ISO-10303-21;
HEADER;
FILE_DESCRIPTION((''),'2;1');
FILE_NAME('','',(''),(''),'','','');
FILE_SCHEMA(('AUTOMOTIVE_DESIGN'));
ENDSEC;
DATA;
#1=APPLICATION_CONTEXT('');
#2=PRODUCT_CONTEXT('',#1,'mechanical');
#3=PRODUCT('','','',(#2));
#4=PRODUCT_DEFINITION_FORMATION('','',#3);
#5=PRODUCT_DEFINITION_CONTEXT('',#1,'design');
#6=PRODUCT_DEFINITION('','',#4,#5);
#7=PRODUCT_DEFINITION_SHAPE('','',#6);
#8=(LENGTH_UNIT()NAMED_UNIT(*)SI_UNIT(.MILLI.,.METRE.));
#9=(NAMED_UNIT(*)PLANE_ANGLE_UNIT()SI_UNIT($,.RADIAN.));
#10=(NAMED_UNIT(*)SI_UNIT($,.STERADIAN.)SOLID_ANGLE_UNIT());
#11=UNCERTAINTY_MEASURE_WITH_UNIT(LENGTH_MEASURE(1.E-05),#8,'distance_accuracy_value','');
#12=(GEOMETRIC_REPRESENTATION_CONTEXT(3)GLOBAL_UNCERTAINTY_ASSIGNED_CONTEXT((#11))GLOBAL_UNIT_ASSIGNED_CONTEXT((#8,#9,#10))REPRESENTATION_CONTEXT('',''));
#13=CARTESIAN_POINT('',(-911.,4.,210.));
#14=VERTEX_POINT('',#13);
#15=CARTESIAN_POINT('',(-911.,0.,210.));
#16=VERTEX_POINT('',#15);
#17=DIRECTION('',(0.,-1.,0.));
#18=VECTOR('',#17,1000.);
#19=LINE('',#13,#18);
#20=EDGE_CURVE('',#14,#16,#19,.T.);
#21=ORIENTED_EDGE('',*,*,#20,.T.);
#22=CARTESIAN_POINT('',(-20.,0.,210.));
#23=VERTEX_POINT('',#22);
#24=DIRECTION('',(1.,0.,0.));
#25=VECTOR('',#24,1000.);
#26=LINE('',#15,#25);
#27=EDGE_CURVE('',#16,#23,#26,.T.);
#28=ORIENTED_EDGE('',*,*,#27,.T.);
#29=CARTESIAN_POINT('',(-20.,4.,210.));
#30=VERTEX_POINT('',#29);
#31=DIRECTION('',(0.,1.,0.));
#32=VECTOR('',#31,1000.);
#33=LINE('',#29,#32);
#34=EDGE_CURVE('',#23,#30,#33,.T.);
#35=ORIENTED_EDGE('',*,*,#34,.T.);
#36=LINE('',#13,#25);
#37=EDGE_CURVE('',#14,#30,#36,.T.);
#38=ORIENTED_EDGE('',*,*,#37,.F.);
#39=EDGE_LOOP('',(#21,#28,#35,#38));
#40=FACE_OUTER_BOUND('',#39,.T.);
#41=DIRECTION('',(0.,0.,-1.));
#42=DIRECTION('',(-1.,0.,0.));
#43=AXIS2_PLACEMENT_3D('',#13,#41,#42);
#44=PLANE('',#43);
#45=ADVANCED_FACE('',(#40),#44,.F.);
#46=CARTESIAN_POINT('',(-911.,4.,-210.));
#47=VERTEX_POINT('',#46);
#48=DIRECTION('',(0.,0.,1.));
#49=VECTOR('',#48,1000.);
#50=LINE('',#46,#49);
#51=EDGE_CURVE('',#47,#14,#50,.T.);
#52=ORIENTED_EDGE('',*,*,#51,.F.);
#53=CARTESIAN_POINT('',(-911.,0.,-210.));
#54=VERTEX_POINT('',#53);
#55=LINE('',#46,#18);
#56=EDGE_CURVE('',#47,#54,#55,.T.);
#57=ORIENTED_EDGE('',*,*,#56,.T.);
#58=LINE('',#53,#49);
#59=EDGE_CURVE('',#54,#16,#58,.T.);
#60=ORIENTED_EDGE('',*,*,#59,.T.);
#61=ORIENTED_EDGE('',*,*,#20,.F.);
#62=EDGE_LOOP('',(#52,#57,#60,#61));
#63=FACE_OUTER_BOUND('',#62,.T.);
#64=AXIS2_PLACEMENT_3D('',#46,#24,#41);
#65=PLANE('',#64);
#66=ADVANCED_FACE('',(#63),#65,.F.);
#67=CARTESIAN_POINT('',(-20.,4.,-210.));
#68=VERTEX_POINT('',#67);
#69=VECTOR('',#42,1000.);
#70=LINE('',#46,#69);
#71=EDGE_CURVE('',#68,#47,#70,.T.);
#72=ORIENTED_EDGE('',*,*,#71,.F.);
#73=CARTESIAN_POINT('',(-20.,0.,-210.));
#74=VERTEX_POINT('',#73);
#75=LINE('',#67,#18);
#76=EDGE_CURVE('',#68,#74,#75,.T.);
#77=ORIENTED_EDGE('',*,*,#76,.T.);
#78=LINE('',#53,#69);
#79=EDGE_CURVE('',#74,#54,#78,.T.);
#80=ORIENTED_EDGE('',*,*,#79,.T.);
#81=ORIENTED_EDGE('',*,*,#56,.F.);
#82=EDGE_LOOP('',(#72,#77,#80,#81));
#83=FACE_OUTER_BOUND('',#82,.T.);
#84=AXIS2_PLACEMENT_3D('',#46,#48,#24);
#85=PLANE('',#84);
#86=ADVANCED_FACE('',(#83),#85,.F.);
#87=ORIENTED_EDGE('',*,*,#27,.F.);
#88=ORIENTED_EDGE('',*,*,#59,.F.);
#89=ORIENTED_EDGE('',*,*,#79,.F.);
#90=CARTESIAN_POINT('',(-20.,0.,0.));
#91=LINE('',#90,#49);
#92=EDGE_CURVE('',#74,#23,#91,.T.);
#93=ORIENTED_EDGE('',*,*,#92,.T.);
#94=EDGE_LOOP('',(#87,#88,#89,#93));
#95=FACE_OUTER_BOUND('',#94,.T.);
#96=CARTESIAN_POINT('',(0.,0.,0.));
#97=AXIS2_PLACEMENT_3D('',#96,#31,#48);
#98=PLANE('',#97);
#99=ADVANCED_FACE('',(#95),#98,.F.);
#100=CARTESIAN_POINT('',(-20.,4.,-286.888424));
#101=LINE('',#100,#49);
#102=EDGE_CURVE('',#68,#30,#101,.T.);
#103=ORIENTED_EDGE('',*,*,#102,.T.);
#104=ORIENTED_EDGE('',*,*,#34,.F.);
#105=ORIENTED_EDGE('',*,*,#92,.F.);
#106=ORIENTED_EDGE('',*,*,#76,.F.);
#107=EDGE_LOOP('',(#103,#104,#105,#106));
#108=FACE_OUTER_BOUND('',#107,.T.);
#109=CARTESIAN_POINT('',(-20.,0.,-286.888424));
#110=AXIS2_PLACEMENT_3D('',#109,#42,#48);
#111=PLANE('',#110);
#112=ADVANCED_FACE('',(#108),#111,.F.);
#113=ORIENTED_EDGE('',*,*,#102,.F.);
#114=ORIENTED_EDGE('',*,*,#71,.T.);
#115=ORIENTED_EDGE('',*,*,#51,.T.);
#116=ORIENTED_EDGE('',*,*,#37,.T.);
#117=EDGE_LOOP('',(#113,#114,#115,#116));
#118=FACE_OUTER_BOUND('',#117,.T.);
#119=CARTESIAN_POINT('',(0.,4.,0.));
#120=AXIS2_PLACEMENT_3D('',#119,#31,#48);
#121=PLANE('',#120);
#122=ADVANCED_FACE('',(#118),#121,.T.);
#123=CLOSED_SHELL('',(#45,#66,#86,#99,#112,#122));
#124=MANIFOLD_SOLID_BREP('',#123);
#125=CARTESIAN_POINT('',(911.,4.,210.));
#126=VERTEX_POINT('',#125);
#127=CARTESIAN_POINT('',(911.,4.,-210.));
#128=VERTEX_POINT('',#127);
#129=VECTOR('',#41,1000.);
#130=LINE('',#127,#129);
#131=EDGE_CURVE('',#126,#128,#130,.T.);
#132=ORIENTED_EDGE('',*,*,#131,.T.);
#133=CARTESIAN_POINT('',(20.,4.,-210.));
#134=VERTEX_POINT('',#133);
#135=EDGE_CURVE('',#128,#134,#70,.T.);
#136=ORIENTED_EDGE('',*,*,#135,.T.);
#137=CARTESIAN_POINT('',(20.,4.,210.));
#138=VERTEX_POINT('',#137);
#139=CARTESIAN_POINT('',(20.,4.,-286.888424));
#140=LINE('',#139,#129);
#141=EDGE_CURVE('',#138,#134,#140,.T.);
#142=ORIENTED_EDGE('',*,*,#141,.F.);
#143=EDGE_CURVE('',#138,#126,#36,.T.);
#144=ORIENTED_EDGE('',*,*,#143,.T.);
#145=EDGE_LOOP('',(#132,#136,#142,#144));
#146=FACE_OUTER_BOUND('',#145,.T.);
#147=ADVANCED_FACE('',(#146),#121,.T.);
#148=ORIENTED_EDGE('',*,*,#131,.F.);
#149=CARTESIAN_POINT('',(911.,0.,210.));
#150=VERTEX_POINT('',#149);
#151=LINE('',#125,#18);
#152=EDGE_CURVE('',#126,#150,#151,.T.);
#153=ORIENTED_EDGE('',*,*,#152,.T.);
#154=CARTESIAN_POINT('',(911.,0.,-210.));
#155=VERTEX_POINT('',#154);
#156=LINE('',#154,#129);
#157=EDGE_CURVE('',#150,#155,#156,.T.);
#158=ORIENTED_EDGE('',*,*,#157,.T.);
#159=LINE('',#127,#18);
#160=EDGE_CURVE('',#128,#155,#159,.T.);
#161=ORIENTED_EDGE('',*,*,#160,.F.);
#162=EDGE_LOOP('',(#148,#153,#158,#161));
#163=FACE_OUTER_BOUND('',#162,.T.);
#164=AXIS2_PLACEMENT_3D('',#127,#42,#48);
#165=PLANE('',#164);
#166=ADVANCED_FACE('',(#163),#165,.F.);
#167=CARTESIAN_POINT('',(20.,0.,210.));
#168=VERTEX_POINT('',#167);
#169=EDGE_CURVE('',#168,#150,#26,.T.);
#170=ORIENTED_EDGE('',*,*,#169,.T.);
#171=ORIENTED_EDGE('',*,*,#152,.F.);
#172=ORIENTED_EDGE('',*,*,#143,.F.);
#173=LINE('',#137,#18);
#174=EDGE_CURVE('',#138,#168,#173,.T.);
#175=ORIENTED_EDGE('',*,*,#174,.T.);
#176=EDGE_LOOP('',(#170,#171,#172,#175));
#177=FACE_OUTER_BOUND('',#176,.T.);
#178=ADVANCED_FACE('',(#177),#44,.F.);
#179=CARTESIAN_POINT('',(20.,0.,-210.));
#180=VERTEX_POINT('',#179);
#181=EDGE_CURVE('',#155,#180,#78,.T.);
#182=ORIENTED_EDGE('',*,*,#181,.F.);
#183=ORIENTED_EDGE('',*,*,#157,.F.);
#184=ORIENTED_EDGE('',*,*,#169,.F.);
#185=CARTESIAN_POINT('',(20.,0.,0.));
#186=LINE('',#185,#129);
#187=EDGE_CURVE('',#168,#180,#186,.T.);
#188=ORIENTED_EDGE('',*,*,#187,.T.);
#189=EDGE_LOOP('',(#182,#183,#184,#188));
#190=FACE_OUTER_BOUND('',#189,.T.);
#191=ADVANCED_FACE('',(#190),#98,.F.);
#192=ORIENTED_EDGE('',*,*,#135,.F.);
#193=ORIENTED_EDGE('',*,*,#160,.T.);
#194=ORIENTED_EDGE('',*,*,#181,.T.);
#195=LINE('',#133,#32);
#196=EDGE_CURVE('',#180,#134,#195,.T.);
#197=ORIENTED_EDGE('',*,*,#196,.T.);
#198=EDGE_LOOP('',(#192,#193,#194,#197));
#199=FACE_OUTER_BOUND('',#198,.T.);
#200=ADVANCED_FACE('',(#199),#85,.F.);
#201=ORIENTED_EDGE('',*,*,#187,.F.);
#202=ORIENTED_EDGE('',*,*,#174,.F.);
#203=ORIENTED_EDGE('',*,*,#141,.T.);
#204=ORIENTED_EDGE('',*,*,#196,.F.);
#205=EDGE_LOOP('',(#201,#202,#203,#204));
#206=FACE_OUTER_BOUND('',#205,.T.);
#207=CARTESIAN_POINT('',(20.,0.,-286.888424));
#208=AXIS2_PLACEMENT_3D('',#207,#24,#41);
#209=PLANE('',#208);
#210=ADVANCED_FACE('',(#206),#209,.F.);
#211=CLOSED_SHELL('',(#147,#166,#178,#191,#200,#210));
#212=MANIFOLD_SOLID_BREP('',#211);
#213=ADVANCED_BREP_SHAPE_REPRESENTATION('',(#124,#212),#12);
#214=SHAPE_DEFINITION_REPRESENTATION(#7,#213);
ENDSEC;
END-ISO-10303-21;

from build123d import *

# Parameters (mm, degrees)
SKETCH1_W           = 1822
SKETCH1_H           = 420
BOSS_EXTRUDE1_DEPTH = 4
SKETCH7_W           = 40
SKETCH7_H           = 573.776848342
CUT_EXTRUDE5_DEPTH  = 935.899459835


with BuildPart() as part:
    # Sketch1 → Boss-Extrude1 (new body)
    with BuildSketch(Plane(origin=(0, 0, 0), x_dir=(1, 0, 0), z_dir=(0, 1, 0))):
        Rectangle(SKETCH1_W, SKETCH1_H)
    extrude(amount=BOSS_EXTRUDE1_DEPTH)

    # Sketch7 → Cut-Extrude5 (cut, through all)
    with BuildSketch(Plane(origin=(0, 4, 0), x_dir=(1, 0, 0), z_dir=(0, 1, 0))):
        Rectangle(SKETCH7_W, SKETCH7_H)
    extrude(amount=-CUT_EXTRUDE5_DEPTH, mode=Mode.SUBTRACT)


with BuildPart() as cut_extrude5_piece_1:
    # of the separate pieces the step leaves, piece 1, a body of its own (cut_extrude5_pieces)
    add(part.part.solids().sort_by_distance((-911, 0, -210))[0])


with BuildPart() as cut_extrude5_piece_2:
    # of the separate pieces the step leaves, piece 2, a body of its own (cut_extrude5_pieces)
    add(part.part.solids().sort_by_distance((20, 0, -210))[0])


solid = Compound([cut_extrude5_piece_1.part, cut_extrude5_piece_2.part])
